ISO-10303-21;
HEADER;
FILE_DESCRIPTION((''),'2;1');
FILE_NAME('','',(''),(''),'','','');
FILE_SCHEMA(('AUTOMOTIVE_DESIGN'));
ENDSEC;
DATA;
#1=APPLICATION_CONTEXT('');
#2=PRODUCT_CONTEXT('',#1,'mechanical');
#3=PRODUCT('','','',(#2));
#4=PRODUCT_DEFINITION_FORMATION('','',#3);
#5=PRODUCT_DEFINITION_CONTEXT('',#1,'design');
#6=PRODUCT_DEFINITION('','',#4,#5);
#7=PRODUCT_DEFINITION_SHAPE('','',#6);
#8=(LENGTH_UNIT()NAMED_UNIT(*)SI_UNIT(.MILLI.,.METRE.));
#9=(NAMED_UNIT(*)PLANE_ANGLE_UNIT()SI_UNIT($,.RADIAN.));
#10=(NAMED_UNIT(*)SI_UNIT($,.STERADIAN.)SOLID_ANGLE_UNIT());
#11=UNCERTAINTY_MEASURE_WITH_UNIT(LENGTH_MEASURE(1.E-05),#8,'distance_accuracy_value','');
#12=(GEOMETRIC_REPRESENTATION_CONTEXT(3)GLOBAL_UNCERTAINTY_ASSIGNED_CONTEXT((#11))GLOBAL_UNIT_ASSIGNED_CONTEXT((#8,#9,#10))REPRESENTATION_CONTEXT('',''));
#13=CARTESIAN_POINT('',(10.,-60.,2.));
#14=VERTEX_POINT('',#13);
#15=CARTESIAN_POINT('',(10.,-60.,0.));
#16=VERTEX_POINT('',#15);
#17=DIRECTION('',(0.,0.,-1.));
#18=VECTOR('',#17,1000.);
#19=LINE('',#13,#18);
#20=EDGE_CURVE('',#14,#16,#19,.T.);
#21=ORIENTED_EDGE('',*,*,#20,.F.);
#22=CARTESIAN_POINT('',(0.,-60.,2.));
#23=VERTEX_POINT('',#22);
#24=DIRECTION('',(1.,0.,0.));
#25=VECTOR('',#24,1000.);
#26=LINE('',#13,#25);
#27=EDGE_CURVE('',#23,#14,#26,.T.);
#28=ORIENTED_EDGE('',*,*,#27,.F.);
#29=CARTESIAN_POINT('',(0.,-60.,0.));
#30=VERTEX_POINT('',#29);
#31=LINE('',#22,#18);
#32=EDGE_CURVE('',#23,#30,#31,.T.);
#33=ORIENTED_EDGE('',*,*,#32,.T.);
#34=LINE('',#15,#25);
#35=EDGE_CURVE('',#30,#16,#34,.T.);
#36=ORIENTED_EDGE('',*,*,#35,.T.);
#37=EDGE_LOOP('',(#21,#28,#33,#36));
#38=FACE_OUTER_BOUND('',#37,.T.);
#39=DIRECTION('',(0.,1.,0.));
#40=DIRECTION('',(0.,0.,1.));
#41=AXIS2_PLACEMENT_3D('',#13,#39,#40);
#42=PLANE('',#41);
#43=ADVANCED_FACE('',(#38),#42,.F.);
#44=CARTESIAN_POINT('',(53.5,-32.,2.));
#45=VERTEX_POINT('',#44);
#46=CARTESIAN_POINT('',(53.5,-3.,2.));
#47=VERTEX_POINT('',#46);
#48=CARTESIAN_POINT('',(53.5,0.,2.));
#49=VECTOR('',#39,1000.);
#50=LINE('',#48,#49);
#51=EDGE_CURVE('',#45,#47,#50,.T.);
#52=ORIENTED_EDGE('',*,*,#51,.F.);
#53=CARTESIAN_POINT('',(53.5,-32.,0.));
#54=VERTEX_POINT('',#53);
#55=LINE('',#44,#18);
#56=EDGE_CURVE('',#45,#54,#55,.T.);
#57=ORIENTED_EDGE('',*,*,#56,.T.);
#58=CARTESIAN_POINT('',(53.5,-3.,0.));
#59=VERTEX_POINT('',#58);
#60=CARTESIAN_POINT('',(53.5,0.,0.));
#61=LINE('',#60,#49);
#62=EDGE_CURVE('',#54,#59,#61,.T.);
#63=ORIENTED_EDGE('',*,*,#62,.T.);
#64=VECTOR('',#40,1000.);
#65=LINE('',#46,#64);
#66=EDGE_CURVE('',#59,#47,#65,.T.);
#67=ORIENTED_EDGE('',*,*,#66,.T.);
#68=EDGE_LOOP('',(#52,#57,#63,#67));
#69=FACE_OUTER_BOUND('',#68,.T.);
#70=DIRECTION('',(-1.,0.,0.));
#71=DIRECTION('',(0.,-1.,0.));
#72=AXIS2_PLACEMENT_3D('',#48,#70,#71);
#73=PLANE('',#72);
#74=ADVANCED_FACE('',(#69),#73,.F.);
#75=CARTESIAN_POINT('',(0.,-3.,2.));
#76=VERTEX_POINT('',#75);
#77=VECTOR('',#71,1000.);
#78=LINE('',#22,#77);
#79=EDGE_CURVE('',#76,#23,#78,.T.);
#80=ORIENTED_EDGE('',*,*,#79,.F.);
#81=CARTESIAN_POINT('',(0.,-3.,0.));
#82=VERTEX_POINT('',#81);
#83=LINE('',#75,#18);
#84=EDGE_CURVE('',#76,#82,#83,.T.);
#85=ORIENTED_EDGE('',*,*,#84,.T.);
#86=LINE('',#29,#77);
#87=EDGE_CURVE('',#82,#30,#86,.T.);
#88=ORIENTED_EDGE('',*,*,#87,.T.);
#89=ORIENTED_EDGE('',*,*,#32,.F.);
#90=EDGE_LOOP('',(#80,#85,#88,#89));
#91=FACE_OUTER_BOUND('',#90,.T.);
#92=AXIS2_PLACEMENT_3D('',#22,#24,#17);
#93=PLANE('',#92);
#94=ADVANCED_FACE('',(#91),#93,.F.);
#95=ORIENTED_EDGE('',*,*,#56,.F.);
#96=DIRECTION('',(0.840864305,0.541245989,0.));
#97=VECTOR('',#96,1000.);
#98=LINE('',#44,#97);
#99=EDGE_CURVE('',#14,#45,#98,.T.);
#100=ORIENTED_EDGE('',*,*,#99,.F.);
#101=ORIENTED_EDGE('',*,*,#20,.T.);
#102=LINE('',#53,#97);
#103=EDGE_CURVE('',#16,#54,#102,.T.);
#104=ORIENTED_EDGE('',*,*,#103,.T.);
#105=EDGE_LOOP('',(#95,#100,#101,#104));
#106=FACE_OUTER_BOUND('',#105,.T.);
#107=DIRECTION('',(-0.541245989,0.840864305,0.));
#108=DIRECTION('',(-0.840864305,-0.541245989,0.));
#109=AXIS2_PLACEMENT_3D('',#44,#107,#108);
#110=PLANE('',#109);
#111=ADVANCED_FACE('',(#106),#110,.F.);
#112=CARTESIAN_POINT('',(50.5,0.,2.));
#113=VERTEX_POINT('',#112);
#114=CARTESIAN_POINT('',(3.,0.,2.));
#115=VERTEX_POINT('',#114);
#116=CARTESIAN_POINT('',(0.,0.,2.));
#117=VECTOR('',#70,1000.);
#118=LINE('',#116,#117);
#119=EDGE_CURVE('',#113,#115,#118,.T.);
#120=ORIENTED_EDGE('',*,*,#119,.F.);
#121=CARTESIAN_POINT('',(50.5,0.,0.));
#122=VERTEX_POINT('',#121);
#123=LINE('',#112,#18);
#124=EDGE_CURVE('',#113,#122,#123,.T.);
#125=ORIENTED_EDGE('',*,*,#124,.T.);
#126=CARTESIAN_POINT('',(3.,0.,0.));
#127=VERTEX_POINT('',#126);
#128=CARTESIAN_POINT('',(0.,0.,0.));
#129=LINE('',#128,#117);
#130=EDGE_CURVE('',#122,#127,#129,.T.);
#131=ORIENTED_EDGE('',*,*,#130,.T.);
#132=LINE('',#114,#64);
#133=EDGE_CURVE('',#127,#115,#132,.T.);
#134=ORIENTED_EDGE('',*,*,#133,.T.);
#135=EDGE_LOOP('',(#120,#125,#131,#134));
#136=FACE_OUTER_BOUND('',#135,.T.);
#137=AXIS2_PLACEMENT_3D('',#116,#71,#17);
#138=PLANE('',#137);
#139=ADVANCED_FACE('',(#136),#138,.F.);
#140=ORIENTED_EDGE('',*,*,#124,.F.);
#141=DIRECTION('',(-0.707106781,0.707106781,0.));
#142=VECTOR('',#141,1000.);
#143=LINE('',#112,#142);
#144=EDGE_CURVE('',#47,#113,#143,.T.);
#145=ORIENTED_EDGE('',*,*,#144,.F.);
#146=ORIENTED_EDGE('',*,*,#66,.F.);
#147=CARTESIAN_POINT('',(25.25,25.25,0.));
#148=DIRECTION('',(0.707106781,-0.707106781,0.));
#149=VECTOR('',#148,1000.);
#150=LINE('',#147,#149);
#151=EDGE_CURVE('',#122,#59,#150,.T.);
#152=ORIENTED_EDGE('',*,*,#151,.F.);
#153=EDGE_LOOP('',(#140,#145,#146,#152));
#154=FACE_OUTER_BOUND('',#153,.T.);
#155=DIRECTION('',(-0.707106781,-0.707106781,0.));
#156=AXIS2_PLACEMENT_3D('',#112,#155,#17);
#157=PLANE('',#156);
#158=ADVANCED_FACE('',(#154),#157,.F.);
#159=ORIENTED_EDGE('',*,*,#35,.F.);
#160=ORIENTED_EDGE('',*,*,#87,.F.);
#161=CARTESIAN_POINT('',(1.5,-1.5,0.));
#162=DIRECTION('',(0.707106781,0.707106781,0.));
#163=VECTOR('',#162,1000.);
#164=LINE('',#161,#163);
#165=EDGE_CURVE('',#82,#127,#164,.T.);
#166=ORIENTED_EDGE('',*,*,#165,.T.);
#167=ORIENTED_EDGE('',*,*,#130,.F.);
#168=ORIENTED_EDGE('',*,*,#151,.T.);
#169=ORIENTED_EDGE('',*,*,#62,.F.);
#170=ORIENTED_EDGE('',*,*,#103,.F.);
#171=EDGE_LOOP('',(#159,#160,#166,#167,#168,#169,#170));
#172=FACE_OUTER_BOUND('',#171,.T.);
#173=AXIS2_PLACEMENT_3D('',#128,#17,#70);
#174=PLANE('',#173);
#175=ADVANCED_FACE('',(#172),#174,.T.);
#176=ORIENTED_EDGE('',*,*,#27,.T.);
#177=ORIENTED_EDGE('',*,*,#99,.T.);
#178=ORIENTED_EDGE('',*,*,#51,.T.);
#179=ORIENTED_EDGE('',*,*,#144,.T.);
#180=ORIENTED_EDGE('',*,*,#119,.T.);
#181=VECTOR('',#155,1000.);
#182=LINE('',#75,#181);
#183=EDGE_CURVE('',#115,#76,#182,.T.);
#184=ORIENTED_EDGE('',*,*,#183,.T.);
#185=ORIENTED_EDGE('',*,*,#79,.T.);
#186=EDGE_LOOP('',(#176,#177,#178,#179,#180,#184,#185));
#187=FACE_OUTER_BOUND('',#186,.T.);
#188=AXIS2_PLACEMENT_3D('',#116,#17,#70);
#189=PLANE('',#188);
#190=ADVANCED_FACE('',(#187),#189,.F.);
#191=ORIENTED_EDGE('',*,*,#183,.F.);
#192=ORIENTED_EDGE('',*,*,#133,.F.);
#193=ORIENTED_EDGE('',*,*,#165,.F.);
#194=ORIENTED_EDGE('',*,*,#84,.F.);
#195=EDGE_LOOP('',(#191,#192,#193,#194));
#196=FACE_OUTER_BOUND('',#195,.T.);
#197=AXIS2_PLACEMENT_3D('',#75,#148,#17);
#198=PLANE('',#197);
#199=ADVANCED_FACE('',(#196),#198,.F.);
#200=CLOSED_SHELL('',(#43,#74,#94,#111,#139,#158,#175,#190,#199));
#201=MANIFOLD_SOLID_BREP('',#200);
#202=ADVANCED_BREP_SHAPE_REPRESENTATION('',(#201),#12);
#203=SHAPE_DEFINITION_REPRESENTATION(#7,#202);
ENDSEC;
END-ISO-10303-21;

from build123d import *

# Parameters (mm, degrees)
EXTRUDE_1_DEPTH = 2
CHAMFER_1_SIZE  = 3


with BuildPart() as part:
    # 草图1 → 凸台-拉伸1 (new body)
    with BuildSketch(Plane.XY):
        Polygon((0, 0), (53.5, 0), (53.5, -32), (10, -60), (0, -60), align=None)
    extrude(amount=EXTRUDE_1_DEPTH)

    # 倒角1
    chamfer_1_edges = [part.edges().sort_by_distance(p)[0] for p in [
        (0, 0, 1),
        (53.5, 0, 1),
    ]]
    chamfer(chamfer_1_edges, length=CHAMFER_1_SIZE)


solid = part.part
